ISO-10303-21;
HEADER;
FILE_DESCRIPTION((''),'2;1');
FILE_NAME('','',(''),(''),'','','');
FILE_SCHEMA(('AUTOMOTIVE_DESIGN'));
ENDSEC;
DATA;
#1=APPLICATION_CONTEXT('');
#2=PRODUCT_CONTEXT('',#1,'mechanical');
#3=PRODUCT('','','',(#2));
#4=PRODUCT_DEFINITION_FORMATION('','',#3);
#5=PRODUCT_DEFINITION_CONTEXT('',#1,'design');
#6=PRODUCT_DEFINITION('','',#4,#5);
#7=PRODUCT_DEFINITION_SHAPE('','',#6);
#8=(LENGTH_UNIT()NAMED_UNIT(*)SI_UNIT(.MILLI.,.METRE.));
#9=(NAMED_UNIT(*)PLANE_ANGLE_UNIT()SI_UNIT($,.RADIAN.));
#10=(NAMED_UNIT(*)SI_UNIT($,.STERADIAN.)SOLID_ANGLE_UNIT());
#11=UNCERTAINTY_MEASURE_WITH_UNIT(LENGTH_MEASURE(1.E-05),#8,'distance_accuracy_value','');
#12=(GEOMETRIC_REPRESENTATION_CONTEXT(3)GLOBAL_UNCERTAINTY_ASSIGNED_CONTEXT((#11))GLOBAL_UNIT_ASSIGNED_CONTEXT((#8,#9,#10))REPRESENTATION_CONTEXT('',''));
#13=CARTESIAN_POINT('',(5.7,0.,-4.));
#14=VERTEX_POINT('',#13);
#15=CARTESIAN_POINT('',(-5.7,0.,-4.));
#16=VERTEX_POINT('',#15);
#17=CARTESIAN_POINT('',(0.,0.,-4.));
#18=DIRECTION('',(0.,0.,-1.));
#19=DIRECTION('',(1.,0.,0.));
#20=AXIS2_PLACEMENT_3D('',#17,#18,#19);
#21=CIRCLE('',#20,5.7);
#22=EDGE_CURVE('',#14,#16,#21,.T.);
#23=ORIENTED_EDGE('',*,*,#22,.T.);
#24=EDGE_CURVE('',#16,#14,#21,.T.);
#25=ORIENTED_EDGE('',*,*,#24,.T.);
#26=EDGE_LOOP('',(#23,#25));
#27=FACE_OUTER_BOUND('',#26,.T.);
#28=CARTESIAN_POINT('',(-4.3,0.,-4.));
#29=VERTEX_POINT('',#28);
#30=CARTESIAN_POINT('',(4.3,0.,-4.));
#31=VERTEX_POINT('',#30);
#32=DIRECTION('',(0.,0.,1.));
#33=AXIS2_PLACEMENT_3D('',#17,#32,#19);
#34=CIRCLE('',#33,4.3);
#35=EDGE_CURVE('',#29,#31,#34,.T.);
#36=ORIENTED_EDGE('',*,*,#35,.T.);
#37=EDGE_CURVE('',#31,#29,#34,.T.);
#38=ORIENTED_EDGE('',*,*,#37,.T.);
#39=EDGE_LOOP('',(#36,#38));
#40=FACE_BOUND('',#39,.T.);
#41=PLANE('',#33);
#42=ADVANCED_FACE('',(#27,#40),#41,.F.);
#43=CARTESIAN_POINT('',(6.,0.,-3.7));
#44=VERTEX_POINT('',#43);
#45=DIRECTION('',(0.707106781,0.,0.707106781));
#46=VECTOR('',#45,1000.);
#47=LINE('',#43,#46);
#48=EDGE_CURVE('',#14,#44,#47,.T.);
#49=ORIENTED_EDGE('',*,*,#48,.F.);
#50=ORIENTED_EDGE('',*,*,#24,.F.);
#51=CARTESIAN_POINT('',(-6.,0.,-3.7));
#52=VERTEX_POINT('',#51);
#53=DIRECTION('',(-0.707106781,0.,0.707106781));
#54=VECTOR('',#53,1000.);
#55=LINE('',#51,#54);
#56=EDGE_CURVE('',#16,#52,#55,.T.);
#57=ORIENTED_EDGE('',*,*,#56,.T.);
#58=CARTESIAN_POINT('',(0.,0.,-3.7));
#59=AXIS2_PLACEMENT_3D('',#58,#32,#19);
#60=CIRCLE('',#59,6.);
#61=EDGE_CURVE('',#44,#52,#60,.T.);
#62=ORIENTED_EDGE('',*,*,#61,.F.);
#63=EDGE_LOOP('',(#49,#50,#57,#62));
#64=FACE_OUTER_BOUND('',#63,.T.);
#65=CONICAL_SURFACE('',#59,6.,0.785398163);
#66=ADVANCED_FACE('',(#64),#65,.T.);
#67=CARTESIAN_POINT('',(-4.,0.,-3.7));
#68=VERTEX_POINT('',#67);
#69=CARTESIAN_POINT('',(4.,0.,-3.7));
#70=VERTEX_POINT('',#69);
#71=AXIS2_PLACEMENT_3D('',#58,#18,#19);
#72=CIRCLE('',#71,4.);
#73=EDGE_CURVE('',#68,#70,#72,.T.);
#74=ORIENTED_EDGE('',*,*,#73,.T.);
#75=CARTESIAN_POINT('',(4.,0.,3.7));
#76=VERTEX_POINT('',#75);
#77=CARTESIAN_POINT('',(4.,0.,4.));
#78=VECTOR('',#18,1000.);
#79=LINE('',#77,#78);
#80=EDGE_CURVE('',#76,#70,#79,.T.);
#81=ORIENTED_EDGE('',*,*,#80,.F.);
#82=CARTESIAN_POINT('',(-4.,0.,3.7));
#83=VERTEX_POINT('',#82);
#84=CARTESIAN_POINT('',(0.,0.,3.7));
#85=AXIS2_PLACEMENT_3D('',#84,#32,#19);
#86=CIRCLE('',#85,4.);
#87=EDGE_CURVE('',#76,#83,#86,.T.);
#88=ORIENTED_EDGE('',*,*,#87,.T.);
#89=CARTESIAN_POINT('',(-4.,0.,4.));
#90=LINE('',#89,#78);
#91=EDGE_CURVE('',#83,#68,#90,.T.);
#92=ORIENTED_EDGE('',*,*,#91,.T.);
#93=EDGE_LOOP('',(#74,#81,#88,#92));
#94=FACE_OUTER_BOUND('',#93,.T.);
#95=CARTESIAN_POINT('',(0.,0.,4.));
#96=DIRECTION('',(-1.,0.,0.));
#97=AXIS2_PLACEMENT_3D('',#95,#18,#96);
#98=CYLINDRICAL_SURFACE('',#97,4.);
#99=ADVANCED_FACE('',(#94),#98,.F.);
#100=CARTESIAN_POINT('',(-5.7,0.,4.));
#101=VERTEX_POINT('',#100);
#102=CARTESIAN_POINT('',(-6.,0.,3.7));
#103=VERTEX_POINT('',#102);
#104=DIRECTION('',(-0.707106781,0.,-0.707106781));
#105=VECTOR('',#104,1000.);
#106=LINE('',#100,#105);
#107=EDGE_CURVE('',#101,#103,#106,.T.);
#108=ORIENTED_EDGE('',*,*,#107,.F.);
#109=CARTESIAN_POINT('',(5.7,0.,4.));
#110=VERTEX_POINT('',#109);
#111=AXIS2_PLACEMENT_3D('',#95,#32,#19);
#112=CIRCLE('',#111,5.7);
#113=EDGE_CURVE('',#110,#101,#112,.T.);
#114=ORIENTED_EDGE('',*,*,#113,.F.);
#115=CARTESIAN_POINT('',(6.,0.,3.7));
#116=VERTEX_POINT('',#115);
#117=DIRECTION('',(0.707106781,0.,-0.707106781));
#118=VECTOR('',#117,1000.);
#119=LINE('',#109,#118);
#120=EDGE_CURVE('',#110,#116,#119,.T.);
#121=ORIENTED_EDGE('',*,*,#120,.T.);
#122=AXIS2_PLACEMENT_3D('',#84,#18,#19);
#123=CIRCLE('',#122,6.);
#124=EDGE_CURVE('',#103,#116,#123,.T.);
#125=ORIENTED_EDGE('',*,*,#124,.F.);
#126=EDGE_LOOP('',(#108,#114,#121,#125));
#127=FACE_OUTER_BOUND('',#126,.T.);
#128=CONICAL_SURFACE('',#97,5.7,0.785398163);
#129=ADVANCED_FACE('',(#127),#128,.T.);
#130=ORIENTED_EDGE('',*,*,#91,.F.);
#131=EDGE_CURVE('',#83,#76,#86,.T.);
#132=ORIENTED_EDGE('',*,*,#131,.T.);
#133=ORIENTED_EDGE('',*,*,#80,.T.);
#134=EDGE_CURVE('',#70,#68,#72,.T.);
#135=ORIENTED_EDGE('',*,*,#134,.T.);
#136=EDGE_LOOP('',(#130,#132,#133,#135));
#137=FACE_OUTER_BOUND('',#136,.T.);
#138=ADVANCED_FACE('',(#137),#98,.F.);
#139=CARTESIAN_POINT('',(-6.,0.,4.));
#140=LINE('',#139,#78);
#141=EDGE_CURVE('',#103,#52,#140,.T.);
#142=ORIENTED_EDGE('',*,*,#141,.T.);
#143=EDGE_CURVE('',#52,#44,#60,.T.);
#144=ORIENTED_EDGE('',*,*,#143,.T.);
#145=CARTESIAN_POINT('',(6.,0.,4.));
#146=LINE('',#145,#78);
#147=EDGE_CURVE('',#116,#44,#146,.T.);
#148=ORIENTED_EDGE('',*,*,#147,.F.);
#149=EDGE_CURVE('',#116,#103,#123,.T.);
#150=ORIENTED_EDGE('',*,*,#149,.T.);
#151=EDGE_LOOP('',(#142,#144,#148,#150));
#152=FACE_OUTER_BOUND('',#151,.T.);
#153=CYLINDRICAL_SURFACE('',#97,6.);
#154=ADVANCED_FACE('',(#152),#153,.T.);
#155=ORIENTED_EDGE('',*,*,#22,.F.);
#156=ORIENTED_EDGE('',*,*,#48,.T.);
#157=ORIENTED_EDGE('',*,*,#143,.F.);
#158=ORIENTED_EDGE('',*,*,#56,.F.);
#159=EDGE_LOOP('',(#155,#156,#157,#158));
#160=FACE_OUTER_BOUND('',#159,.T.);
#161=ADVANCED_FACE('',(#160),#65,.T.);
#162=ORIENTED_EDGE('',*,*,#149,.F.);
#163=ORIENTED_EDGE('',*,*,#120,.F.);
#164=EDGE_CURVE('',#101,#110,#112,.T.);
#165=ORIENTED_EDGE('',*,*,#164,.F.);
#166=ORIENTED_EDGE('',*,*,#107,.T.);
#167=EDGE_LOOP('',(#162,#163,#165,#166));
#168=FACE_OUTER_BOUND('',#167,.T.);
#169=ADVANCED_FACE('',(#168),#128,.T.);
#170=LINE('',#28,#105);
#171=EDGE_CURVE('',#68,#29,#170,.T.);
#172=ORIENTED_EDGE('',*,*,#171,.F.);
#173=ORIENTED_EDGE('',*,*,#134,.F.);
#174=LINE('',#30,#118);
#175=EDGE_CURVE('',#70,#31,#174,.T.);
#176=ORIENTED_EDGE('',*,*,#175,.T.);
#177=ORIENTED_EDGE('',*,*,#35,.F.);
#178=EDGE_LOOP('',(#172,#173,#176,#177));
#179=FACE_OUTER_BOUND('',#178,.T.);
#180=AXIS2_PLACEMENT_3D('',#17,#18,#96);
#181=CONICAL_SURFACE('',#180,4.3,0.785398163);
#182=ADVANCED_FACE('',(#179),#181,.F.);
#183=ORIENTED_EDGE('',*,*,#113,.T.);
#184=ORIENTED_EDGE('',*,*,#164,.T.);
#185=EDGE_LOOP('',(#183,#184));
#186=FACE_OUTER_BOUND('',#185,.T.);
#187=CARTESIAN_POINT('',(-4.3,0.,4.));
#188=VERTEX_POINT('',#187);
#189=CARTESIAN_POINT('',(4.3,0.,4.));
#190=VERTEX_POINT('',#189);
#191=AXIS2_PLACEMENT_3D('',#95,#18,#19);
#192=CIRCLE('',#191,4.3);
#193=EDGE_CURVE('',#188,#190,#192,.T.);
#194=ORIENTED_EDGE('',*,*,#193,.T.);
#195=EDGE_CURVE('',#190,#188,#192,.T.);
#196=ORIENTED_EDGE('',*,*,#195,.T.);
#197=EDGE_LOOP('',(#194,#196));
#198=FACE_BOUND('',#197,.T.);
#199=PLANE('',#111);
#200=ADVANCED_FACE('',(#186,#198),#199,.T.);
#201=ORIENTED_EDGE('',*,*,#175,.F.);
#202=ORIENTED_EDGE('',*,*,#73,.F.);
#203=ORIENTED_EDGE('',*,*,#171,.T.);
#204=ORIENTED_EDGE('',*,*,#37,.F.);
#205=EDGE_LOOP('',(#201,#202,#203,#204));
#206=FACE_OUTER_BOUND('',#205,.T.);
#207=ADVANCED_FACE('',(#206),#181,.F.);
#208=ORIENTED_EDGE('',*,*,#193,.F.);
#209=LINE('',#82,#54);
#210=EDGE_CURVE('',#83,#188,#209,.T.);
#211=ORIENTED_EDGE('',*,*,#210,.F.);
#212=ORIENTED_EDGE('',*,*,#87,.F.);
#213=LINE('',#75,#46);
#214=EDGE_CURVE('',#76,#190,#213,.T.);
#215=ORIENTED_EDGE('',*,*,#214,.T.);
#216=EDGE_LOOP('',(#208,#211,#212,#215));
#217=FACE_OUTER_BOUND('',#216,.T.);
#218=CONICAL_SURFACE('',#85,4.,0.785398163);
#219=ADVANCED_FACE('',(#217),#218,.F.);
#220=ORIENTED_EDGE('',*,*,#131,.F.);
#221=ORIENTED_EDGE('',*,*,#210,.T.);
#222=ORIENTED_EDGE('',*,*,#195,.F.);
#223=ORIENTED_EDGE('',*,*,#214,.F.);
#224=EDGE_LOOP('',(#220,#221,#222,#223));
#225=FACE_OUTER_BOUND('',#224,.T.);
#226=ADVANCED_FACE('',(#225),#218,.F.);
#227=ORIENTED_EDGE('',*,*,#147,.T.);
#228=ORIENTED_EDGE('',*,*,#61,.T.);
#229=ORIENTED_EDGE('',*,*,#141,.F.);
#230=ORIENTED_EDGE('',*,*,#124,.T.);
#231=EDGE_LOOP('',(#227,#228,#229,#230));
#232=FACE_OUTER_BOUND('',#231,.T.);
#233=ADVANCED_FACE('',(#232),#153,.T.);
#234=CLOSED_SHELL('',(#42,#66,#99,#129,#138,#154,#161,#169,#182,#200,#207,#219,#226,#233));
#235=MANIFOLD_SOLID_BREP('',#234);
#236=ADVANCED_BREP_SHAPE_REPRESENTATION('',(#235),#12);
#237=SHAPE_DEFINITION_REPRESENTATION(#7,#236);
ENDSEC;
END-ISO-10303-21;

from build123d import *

# Parameters (mm, degrees)
SKETCH_1_R      = 6
SKETCH_1_R_2    = 4
EXTRUDE_1_DEPTH = 4
CHAMFER_1_SIZE  = 0.3


with BuildPart() as part:
    # 草图1 → 凸台-拉伸1 (new, symmetric)
    with BuildSketch(Plane.XY):
        Circle(SKETCH_1_R)
        Circle(SKETCH_1_R_2, mode=Mode.SUBTRACT)
    extrude(amount=EXTRUDE_1_DEPTH, both=True)

    # 倒角1
    chamfer_1_edges = [part.edges().sort_by_distance(p)[0] for p in [
        (-6, 0, -4),
        (-6, 0, 4),
        (-4, 0, -4),
        (-4, 0, 4),
    ]]
    chamfer(chamfer_1_edges, length=CHAMFER_1_SIZE)


solid = part.part
